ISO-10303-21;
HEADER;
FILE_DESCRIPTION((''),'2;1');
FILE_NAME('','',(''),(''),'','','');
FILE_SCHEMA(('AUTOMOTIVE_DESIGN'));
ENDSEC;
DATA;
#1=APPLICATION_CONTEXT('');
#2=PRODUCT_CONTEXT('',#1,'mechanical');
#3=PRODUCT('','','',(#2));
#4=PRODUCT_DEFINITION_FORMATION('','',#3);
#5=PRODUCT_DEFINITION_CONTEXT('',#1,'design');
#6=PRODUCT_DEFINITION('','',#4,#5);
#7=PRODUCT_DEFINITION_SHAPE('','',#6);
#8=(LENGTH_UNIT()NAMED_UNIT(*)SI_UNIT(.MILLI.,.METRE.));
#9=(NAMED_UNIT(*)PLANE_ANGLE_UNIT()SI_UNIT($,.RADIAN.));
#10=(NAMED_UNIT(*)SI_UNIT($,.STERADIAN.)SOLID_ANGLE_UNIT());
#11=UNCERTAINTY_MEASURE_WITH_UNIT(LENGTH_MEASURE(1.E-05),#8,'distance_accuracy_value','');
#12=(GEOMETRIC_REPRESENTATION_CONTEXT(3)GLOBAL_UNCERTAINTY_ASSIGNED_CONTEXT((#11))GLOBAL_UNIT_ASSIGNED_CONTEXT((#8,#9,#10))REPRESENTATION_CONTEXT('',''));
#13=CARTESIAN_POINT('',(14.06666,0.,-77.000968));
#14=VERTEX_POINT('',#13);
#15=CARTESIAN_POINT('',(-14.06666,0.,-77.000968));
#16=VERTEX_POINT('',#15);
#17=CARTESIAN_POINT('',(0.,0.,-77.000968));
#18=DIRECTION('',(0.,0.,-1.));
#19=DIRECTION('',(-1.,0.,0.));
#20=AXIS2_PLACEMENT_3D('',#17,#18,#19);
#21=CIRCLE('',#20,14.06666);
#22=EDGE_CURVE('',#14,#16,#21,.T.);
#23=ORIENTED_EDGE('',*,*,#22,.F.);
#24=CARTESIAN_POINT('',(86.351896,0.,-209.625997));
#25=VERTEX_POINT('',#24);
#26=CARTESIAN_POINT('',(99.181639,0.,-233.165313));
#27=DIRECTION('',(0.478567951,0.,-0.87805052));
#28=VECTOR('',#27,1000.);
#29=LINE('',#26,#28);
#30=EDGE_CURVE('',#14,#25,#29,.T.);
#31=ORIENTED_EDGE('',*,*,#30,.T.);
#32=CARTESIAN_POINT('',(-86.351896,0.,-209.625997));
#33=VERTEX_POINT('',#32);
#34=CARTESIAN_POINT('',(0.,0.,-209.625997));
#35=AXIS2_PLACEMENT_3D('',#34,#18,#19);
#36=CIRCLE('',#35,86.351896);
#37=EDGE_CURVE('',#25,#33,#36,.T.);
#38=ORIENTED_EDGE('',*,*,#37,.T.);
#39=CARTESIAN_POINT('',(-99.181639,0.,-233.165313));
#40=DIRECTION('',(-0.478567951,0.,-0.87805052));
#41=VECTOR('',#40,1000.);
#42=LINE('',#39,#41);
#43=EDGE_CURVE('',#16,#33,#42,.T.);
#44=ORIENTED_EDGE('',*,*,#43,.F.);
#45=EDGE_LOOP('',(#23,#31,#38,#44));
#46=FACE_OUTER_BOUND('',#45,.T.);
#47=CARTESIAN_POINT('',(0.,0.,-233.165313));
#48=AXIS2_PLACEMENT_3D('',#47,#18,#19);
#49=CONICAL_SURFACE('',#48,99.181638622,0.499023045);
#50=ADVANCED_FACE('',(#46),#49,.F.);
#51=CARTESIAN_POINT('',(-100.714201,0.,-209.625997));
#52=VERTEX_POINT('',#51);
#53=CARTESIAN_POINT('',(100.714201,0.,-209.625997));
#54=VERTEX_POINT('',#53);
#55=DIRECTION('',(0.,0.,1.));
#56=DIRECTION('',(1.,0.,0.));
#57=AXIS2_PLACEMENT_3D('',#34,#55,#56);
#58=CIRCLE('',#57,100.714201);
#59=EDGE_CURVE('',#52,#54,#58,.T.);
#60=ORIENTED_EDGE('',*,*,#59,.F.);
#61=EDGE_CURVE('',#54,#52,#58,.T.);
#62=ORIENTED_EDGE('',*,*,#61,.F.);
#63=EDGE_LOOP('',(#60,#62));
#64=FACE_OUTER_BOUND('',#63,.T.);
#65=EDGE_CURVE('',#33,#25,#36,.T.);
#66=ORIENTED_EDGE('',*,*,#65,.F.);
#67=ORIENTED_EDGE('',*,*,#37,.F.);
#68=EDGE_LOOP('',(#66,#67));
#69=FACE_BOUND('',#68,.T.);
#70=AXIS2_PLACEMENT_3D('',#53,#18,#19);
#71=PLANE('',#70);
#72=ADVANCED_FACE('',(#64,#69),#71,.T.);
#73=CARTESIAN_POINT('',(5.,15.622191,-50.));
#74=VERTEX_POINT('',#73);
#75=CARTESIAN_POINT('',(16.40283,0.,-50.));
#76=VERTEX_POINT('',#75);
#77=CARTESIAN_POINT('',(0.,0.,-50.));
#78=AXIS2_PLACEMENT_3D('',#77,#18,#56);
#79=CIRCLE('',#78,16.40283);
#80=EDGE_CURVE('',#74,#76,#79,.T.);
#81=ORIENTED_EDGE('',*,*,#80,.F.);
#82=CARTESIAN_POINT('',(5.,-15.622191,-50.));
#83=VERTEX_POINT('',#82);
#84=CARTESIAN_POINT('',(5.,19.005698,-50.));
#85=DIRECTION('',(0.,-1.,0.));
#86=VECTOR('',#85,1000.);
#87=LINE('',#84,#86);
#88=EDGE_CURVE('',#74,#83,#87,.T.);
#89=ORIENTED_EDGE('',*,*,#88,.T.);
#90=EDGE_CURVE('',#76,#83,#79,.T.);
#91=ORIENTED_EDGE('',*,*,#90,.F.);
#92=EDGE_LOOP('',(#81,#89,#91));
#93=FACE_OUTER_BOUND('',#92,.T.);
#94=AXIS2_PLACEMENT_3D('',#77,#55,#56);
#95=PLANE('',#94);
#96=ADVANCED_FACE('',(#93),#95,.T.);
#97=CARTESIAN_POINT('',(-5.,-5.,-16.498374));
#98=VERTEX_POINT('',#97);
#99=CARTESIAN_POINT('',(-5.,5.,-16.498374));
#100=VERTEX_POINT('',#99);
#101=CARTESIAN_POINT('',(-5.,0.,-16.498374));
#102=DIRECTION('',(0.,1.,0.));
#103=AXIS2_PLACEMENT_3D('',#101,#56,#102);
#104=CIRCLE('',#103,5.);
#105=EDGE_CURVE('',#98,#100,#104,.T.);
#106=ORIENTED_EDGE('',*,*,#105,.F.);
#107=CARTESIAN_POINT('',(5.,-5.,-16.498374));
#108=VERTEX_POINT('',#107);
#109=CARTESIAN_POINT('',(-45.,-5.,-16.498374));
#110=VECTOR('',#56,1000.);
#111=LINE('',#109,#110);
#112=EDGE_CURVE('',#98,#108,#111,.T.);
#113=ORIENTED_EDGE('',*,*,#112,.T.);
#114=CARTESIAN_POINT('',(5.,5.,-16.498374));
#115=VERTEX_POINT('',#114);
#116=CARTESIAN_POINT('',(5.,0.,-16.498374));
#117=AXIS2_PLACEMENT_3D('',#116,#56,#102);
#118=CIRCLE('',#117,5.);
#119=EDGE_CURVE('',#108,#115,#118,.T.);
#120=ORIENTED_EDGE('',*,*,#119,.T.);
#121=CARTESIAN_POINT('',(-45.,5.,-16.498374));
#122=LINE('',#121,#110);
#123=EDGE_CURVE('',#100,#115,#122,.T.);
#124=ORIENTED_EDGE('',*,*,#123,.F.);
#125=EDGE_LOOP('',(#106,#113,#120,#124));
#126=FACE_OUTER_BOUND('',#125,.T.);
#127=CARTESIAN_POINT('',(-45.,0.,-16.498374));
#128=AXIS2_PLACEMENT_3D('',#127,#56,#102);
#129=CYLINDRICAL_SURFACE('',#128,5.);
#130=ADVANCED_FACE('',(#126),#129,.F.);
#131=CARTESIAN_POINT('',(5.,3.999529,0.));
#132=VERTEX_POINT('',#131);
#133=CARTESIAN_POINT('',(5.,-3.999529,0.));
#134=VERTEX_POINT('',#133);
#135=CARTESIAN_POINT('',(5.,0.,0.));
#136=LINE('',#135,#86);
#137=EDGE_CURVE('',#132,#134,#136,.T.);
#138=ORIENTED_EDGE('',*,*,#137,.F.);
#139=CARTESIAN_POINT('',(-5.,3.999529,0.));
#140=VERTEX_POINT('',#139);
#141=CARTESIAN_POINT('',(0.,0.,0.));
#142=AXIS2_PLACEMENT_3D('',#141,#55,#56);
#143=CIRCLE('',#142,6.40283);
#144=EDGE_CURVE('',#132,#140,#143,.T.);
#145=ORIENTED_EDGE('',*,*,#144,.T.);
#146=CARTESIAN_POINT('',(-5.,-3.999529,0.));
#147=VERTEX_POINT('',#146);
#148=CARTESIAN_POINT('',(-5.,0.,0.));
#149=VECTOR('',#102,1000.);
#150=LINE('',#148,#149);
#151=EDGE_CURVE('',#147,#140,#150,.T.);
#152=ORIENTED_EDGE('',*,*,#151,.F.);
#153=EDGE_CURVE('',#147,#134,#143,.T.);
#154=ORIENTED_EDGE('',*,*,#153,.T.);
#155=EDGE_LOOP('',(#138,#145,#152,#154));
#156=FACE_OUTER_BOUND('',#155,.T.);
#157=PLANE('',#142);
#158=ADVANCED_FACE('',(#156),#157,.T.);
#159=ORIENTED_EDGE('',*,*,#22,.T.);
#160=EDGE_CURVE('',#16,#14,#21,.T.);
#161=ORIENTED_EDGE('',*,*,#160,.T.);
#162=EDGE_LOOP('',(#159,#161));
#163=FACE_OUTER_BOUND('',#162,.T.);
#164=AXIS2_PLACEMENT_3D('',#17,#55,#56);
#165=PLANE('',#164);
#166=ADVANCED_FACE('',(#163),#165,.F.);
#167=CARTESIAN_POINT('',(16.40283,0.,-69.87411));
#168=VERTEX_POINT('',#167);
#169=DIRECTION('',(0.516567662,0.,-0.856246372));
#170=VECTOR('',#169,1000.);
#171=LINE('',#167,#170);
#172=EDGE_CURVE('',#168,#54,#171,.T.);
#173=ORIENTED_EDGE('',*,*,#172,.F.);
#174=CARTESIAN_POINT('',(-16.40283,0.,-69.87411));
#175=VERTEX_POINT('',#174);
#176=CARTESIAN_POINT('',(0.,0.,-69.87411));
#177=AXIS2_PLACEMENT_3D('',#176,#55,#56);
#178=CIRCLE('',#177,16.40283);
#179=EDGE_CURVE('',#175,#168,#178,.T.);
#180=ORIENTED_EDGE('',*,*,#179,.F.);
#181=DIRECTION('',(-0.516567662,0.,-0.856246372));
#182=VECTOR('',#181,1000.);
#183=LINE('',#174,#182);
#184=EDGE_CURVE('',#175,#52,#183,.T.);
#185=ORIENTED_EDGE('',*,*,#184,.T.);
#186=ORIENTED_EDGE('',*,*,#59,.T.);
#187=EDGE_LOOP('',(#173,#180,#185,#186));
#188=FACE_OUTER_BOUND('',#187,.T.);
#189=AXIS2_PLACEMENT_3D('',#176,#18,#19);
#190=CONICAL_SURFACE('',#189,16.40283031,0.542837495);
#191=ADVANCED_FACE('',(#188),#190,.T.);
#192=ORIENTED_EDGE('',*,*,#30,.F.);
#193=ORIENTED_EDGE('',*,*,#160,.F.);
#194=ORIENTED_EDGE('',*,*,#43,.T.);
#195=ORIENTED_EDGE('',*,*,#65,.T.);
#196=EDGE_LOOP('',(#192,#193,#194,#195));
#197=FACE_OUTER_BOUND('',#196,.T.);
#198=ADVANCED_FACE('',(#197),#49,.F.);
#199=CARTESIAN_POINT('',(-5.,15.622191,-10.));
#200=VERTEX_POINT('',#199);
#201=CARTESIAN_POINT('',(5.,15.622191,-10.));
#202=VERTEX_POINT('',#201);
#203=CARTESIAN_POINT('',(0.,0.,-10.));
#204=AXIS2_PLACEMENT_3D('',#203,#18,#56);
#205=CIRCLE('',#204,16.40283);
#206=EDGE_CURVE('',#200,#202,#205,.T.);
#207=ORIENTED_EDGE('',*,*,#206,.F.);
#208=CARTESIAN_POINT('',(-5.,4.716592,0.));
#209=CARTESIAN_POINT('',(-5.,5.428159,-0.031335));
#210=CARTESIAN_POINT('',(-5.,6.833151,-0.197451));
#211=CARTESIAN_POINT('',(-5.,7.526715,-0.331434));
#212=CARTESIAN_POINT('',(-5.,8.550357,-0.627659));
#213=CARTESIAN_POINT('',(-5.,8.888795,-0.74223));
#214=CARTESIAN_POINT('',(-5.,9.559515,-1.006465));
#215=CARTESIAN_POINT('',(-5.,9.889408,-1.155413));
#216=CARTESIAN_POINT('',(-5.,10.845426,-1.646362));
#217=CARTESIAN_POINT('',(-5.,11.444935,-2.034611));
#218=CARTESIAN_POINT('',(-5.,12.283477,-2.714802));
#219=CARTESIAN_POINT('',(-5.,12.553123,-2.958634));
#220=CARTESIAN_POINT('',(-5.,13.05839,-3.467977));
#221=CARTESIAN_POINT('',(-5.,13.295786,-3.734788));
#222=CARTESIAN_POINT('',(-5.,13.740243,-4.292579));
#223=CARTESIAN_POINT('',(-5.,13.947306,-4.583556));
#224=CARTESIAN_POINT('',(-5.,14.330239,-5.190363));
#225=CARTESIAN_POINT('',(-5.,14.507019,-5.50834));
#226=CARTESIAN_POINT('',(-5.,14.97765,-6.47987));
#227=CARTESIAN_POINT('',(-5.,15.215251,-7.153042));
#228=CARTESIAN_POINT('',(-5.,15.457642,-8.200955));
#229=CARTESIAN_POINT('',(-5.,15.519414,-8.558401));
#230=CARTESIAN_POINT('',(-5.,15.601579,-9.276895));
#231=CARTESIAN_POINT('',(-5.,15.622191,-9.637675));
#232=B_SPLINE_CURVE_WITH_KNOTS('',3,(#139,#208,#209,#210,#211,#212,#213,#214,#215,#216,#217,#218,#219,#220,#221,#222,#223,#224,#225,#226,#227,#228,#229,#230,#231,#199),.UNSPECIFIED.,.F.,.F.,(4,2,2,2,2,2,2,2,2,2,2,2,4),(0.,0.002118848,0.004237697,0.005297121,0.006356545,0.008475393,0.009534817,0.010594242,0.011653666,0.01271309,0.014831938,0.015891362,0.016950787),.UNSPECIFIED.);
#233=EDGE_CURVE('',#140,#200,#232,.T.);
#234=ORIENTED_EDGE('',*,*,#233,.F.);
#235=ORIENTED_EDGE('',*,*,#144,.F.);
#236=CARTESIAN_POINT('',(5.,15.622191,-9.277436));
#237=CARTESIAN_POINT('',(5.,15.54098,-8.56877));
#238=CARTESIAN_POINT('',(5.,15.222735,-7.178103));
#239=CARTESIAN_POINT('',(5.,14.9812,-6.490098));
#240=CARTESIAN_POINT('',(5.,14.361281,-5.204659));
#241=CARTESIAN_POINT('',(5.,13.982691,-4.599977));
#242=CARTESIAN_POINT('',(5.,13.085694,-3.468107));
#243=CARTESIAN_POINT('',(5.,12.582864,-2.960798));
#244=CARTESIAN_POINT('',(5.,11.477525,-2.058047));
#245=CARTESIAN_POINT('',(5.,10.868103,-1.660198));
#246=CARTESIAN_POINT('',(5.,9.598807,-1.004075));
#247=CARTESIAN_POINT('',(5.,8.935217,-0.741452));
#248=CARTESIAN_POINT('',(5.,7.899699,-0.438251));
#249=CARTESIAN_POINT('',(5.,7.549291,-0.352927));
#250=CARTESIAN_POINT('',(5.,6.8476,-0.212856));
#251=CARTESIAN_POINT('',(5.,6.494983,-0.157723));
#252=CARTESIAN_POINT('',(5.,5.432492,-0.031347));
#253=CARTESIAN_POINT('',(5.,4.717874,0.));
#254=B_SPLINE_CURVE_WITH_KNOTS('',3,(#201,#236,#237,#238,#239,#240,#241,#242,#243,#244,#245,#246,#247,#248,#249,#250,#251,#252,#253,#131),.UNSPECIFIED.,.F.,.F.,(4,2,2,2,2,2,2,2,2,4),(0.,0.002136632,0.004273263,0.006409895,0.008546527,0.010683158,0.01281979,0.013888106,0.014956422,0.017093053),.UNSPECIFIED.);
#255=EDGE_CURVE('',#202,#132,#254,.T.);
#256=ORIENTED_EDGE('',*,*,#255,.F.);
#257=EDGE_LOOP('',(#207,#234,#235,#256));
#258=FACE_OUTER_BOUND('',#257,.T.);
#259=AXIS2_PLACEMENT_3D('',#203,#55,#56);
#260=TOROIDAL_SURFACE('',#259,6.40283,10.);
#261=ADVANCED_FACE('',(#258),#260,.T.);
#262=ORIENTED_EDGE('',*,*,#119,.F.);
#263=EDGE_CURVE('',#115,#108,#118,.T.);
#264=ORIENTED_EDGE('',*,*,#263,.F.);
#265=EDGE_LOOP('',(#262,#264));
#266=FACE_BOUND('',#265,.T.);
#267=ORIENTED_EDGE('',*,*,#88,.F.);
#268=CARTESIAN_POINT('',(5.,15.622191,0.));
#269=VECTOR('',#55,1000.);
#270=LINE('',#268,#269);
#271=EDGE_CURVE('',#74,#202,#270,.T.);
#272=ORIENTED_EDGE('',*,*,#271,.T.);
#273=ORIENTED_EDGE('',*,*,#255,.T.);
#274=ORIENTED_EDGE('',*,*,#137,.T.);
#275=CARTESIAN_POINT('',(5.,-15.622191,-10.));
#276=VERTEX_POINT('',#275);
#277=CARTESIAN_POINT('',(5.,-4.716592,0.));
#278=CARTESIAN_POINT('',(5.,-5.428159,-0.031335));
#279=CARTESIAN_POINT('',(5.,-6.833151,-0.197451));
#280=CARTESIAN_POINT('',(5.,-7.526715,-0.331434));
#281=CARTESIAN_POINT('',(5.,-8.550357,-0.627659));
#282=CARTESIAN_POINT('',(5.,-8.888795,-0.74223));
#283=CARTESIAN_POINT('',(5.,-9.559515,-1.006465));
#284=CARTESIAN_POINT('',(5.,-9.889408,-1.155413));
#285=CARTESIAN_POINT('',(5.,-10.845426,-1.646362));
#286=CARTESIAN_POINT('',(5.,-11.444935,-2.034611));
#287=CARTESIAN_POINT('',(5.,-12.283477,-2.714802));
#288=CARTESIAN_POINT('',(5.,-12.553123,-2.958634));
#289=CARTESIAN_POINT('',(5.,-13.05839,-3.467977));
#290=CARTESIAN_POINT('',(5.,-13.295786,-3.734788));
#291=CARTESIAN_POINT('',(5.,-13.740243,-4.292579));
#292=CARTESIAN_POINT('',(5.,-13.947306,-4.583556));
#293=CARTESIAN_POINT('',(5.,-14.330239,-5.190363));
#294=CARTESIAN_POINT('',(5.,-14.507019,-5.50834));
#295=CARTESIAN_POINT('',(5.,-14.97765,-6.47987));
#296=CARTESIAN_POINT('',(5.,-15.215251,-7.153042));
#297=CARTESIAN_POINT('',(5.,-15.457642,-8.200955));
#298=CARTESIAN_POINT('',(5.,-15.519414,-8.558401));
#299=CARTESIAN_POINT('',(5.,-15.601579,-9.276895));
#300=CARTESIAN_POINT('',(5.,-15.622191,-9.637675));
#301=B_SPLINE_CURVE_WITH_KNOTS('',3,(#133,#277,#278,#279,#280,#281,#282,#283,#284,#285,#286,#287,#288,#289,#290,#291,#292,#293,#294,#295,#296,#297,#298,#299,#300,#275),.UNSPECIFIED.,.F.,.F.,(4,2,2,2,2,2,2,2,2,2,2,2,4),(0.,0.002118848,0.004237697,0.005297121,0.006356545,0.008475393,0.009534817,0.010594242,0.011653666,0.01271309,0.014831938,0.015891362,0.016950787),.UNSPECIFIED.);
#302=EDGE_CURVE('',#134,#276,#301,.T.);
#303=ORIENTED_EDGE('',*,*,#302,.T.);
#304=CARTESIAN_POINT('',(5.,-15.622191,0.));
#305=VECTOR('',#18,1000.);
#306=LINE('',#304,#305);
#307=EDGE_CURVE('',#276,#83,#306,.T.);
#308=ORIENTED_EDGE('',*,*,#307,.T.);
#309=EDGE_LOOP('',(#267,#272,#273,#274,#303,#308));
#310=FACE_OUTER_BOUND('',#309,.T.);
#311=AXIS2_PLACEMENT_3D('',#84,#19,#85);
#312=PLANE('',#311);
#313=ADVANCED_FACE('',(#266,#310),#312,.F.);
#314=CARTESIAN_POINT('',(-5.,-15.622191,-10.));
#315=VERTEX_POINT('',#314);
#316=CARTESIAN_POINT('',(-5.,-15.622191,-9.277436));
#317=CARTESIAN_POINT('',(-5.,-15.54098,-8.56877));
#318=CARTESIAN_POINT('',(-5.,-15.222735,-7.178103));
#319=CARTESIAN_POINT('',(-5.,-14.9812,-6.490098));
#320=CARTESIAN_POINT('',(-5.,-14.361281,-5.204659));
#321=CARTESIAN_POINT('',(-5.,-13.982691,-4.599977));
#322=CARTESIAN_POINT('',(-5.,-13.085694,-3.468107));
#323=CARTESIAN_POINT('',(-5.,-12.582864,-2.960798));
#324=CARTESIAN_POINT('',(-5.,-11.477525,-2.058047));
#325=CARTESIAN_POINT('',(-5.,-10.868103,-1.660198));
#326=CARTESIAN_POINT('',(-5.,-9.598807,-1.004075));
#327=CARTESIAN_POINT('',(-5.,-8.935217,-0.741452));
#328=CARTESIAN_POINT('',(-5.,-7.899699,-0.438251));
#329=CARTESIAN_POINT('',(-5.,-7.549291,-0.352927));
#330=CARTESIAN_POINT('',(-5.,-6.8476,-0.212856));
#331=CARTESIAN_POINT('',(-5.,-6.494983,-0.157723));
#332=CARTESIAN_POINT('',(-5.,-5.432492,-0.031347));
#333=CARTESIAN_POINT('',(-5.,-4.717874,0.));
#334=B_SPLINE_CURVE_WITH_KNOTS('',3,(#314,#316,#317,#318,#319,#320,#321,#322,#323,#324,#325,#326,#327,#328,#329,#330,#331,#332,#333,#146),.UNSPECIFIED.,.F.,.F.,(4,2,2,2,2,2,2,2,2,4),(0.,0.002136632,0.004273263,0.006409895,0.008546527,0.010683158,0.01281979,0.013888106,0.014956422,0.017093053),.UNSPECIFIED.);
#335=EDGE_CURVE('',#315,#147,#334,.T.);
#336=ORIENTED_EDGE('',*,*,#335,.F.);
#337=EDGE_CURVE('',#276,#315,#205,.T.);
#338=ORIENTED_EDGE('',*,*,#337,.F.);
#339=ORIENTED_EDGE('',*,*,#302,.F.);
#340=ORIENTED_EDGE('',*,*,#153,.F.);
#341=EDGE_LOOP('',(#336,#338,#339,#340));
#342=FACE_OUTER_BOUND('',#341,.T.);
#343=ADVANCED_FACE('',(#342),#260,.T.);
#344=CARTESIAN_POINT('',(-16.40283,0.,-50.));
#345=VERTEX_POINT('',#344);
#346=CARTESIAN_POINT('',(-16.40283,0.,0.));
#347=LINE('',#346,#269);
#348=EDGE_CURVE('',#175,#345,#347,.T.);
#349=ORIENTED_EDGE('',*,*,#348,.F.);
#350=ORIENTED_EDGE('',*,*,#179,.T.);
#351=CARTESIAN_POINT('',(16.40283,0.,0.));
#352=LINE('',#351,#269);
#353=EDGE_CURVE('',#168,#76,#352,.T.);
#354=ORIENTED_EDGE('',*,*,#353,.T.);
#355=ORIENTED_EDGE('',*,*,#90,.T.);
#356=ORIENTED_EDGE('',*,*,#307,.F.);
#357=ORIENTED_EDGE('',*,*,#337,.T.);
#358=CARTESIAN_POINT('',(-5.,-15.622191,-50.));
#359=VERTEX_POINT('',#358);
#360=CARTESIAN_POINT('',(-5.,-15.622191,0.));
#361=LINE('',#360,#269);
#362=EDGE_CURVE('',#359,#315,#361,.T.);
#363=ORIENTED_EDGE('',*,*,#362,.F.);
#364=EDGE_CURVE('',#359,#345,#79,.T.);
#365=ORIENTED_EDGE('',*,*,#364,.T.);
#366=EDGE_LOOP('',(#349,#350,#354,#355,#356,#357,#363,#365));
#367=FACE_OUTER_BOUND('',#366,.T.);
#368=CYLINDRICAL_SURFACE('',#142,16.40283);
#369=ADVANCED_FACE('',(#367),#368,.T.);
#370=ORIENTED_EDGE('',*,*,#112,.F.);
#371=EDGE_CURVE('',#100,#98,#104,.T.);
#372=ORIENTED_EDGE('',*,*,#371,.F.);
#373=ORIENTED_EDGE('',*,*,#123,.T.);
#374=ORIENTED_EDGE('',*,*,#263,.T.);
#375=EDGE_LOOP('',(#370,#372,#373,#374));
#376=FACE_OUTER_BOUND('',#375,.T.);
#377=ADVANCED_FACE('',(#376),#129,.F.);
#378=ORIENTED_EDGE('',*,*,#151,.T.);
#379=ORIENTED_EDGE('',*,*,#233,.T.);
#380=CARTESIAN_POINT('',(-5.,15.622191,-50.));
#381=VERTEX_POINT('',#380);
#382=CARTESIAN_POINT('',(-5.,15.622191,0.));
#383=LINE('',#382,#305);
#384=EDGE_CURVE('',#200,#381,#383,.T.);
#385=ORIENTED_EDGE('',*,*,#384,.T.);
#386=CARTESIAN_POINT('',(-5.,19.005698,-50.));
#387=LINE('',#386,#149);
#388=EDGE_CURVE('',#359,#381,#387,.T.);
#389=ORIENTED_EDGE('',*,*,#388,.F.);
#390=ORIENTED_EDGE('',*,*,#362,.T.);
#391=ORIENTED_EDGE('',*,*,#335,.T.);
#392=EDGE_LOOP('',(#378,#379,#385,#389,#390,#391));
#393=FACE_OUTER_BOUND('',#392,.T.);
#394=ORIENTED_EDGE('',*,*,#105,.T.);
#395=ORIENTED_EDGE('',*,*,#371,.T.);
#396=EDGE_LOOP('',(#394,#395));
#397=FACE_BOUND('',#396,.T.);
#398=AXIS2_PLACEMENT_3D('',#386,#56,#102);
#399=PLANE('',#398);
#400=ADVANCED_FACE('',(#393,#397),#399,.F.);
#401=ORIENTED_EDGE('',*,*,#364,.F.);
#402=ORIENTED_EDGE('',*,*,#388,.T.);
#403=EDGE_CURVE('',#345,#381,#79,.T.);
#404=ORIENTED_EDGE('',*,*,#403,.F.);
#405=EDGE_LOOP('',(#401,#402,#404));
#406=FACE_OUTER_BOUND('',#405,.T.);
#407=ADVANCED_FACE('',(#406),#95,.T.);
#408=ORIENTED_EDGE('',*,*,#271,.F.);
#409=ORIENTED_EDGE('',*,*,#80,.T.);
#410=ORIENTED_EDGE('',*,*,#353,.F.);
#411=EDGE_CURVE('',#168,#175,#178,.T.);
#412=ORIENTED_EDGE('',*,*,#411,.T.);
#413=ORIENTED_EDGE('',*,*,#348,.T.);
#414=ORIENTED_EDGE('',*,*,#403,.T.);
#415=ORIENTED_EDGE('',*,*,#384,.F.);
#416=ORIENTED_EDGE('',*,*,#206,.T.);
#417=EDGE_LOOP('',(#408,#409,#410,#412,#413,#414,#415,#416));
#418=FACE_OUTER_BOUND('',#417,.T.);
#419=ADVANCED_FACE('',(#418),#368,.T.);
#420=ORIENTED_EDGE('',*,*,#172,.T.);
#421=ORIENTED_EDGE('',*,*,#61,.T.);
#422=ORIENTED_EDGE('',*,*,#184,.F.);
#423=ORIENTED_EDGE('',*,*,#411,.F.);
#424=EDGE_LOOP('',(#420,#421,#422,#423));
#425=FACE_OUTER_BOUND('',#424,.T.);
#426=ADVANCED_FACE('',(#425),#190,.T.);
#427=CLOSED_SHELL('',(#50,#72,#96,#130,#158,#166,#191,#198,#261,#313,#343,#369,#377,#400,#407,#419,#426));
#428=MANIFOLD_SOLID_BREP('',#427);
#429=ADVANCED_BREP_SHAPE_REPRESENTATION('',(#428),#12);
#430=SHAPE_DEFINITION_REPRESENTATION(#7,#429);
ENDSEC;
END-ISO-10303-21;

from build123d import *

# Parameters (mm, degrees)
SKETCH2_W          = 22.958469665
SKETCH2_H          = 42.577525561
CUT_EXTRUDE1_DEPTH = 50
SKETCH3_R          = 5
CUT_EXTRUDE2_DEPTH = 50
FILLET1_R          = 10


with BuildPart() as part:
    # Sketch1 → Revolve1 (revolve)
    with BuildSketch(Plane(origin=(0, 0, 0), x_dir=(1, 0, 0), z_dir=(0, 1, 0)), mode=Mode.PRIVATE) as revolve1_sk:
        Polygon((0, 0), (16.40283031, 0), (16.40283031, 69.874110237), (100.714201253, 209.625997087), (8.201415155, 209.625997087), (0, 209.625997087), align=None)
    revolve(revolve1_sk.sketch.rotate(Axis((0, 0, 0), (0, 0, -1)), 180), axis=Axis((0, 0, 0), (0, 0, -1)))

    # Sketch2 → Cut-Extrude1 (cut)
    with BuildSketch(Plane.XY):
        with Locations((-16.479234833, -2.283064826)):
            Rectangle(SKETCH2_W, SKETCH2_H)
        with Locations((16.479234833, -2.283064826)):
            Rectangle(SKETCH2_W, SKETCH2_H)
    extrude(amount=-CUT_EXTRUDE1_DEPTH, mode=Mode.SUBTRACT)

    # Sketch3 → Cut-Extrude2 (cut)
    with BuildSketch(Plane(origin=(5, 0, 0), x_dir=(0, 0, -1), z_dir=(1, 0, 0))):
        with Locations(Location((16.498374342, 0, 0), (0, 0, 90))):
            Circle(SKETCH3_R)
    extrude(amount=-CUT_EXTRUDE2_DEPTH, mode=Mode.SUBTRACT)

    # Fillet1
    fillet1_edges = [part.edges().sort_by_distance(p)[0] for p in [
        (0, -16.40283031, 0),
        (0, 16.40283031, 0),
    ]]
    fillet(fillet1_edges, radius=FILLET1_R)

    # Sketch4 → Cut-Revolve1 (revolve, cut)
    with BuildSketch(Plane(origin=(0, 0, 0), x_dir=(0, 0, -1), z_dir=(1, 0, 0)), mode=Mode.PRIVATE) as cut_revolve1_sk:
        Polygon((77.000967597, 14.066660466), (233.165313112, 99.181638622), (233.165313112, 0), (77.000967597, 0), align=None)
    revolve(cut_revolve1_sk.sketch.rotate(Axis((0, 0, -233.165313112), (0, 0, 1)), 197.747662393), axis=Axis((0, 0, -233.165313112), (0, 0, 1)), mode=Mode.SUBTRACT)


solid = part.part
